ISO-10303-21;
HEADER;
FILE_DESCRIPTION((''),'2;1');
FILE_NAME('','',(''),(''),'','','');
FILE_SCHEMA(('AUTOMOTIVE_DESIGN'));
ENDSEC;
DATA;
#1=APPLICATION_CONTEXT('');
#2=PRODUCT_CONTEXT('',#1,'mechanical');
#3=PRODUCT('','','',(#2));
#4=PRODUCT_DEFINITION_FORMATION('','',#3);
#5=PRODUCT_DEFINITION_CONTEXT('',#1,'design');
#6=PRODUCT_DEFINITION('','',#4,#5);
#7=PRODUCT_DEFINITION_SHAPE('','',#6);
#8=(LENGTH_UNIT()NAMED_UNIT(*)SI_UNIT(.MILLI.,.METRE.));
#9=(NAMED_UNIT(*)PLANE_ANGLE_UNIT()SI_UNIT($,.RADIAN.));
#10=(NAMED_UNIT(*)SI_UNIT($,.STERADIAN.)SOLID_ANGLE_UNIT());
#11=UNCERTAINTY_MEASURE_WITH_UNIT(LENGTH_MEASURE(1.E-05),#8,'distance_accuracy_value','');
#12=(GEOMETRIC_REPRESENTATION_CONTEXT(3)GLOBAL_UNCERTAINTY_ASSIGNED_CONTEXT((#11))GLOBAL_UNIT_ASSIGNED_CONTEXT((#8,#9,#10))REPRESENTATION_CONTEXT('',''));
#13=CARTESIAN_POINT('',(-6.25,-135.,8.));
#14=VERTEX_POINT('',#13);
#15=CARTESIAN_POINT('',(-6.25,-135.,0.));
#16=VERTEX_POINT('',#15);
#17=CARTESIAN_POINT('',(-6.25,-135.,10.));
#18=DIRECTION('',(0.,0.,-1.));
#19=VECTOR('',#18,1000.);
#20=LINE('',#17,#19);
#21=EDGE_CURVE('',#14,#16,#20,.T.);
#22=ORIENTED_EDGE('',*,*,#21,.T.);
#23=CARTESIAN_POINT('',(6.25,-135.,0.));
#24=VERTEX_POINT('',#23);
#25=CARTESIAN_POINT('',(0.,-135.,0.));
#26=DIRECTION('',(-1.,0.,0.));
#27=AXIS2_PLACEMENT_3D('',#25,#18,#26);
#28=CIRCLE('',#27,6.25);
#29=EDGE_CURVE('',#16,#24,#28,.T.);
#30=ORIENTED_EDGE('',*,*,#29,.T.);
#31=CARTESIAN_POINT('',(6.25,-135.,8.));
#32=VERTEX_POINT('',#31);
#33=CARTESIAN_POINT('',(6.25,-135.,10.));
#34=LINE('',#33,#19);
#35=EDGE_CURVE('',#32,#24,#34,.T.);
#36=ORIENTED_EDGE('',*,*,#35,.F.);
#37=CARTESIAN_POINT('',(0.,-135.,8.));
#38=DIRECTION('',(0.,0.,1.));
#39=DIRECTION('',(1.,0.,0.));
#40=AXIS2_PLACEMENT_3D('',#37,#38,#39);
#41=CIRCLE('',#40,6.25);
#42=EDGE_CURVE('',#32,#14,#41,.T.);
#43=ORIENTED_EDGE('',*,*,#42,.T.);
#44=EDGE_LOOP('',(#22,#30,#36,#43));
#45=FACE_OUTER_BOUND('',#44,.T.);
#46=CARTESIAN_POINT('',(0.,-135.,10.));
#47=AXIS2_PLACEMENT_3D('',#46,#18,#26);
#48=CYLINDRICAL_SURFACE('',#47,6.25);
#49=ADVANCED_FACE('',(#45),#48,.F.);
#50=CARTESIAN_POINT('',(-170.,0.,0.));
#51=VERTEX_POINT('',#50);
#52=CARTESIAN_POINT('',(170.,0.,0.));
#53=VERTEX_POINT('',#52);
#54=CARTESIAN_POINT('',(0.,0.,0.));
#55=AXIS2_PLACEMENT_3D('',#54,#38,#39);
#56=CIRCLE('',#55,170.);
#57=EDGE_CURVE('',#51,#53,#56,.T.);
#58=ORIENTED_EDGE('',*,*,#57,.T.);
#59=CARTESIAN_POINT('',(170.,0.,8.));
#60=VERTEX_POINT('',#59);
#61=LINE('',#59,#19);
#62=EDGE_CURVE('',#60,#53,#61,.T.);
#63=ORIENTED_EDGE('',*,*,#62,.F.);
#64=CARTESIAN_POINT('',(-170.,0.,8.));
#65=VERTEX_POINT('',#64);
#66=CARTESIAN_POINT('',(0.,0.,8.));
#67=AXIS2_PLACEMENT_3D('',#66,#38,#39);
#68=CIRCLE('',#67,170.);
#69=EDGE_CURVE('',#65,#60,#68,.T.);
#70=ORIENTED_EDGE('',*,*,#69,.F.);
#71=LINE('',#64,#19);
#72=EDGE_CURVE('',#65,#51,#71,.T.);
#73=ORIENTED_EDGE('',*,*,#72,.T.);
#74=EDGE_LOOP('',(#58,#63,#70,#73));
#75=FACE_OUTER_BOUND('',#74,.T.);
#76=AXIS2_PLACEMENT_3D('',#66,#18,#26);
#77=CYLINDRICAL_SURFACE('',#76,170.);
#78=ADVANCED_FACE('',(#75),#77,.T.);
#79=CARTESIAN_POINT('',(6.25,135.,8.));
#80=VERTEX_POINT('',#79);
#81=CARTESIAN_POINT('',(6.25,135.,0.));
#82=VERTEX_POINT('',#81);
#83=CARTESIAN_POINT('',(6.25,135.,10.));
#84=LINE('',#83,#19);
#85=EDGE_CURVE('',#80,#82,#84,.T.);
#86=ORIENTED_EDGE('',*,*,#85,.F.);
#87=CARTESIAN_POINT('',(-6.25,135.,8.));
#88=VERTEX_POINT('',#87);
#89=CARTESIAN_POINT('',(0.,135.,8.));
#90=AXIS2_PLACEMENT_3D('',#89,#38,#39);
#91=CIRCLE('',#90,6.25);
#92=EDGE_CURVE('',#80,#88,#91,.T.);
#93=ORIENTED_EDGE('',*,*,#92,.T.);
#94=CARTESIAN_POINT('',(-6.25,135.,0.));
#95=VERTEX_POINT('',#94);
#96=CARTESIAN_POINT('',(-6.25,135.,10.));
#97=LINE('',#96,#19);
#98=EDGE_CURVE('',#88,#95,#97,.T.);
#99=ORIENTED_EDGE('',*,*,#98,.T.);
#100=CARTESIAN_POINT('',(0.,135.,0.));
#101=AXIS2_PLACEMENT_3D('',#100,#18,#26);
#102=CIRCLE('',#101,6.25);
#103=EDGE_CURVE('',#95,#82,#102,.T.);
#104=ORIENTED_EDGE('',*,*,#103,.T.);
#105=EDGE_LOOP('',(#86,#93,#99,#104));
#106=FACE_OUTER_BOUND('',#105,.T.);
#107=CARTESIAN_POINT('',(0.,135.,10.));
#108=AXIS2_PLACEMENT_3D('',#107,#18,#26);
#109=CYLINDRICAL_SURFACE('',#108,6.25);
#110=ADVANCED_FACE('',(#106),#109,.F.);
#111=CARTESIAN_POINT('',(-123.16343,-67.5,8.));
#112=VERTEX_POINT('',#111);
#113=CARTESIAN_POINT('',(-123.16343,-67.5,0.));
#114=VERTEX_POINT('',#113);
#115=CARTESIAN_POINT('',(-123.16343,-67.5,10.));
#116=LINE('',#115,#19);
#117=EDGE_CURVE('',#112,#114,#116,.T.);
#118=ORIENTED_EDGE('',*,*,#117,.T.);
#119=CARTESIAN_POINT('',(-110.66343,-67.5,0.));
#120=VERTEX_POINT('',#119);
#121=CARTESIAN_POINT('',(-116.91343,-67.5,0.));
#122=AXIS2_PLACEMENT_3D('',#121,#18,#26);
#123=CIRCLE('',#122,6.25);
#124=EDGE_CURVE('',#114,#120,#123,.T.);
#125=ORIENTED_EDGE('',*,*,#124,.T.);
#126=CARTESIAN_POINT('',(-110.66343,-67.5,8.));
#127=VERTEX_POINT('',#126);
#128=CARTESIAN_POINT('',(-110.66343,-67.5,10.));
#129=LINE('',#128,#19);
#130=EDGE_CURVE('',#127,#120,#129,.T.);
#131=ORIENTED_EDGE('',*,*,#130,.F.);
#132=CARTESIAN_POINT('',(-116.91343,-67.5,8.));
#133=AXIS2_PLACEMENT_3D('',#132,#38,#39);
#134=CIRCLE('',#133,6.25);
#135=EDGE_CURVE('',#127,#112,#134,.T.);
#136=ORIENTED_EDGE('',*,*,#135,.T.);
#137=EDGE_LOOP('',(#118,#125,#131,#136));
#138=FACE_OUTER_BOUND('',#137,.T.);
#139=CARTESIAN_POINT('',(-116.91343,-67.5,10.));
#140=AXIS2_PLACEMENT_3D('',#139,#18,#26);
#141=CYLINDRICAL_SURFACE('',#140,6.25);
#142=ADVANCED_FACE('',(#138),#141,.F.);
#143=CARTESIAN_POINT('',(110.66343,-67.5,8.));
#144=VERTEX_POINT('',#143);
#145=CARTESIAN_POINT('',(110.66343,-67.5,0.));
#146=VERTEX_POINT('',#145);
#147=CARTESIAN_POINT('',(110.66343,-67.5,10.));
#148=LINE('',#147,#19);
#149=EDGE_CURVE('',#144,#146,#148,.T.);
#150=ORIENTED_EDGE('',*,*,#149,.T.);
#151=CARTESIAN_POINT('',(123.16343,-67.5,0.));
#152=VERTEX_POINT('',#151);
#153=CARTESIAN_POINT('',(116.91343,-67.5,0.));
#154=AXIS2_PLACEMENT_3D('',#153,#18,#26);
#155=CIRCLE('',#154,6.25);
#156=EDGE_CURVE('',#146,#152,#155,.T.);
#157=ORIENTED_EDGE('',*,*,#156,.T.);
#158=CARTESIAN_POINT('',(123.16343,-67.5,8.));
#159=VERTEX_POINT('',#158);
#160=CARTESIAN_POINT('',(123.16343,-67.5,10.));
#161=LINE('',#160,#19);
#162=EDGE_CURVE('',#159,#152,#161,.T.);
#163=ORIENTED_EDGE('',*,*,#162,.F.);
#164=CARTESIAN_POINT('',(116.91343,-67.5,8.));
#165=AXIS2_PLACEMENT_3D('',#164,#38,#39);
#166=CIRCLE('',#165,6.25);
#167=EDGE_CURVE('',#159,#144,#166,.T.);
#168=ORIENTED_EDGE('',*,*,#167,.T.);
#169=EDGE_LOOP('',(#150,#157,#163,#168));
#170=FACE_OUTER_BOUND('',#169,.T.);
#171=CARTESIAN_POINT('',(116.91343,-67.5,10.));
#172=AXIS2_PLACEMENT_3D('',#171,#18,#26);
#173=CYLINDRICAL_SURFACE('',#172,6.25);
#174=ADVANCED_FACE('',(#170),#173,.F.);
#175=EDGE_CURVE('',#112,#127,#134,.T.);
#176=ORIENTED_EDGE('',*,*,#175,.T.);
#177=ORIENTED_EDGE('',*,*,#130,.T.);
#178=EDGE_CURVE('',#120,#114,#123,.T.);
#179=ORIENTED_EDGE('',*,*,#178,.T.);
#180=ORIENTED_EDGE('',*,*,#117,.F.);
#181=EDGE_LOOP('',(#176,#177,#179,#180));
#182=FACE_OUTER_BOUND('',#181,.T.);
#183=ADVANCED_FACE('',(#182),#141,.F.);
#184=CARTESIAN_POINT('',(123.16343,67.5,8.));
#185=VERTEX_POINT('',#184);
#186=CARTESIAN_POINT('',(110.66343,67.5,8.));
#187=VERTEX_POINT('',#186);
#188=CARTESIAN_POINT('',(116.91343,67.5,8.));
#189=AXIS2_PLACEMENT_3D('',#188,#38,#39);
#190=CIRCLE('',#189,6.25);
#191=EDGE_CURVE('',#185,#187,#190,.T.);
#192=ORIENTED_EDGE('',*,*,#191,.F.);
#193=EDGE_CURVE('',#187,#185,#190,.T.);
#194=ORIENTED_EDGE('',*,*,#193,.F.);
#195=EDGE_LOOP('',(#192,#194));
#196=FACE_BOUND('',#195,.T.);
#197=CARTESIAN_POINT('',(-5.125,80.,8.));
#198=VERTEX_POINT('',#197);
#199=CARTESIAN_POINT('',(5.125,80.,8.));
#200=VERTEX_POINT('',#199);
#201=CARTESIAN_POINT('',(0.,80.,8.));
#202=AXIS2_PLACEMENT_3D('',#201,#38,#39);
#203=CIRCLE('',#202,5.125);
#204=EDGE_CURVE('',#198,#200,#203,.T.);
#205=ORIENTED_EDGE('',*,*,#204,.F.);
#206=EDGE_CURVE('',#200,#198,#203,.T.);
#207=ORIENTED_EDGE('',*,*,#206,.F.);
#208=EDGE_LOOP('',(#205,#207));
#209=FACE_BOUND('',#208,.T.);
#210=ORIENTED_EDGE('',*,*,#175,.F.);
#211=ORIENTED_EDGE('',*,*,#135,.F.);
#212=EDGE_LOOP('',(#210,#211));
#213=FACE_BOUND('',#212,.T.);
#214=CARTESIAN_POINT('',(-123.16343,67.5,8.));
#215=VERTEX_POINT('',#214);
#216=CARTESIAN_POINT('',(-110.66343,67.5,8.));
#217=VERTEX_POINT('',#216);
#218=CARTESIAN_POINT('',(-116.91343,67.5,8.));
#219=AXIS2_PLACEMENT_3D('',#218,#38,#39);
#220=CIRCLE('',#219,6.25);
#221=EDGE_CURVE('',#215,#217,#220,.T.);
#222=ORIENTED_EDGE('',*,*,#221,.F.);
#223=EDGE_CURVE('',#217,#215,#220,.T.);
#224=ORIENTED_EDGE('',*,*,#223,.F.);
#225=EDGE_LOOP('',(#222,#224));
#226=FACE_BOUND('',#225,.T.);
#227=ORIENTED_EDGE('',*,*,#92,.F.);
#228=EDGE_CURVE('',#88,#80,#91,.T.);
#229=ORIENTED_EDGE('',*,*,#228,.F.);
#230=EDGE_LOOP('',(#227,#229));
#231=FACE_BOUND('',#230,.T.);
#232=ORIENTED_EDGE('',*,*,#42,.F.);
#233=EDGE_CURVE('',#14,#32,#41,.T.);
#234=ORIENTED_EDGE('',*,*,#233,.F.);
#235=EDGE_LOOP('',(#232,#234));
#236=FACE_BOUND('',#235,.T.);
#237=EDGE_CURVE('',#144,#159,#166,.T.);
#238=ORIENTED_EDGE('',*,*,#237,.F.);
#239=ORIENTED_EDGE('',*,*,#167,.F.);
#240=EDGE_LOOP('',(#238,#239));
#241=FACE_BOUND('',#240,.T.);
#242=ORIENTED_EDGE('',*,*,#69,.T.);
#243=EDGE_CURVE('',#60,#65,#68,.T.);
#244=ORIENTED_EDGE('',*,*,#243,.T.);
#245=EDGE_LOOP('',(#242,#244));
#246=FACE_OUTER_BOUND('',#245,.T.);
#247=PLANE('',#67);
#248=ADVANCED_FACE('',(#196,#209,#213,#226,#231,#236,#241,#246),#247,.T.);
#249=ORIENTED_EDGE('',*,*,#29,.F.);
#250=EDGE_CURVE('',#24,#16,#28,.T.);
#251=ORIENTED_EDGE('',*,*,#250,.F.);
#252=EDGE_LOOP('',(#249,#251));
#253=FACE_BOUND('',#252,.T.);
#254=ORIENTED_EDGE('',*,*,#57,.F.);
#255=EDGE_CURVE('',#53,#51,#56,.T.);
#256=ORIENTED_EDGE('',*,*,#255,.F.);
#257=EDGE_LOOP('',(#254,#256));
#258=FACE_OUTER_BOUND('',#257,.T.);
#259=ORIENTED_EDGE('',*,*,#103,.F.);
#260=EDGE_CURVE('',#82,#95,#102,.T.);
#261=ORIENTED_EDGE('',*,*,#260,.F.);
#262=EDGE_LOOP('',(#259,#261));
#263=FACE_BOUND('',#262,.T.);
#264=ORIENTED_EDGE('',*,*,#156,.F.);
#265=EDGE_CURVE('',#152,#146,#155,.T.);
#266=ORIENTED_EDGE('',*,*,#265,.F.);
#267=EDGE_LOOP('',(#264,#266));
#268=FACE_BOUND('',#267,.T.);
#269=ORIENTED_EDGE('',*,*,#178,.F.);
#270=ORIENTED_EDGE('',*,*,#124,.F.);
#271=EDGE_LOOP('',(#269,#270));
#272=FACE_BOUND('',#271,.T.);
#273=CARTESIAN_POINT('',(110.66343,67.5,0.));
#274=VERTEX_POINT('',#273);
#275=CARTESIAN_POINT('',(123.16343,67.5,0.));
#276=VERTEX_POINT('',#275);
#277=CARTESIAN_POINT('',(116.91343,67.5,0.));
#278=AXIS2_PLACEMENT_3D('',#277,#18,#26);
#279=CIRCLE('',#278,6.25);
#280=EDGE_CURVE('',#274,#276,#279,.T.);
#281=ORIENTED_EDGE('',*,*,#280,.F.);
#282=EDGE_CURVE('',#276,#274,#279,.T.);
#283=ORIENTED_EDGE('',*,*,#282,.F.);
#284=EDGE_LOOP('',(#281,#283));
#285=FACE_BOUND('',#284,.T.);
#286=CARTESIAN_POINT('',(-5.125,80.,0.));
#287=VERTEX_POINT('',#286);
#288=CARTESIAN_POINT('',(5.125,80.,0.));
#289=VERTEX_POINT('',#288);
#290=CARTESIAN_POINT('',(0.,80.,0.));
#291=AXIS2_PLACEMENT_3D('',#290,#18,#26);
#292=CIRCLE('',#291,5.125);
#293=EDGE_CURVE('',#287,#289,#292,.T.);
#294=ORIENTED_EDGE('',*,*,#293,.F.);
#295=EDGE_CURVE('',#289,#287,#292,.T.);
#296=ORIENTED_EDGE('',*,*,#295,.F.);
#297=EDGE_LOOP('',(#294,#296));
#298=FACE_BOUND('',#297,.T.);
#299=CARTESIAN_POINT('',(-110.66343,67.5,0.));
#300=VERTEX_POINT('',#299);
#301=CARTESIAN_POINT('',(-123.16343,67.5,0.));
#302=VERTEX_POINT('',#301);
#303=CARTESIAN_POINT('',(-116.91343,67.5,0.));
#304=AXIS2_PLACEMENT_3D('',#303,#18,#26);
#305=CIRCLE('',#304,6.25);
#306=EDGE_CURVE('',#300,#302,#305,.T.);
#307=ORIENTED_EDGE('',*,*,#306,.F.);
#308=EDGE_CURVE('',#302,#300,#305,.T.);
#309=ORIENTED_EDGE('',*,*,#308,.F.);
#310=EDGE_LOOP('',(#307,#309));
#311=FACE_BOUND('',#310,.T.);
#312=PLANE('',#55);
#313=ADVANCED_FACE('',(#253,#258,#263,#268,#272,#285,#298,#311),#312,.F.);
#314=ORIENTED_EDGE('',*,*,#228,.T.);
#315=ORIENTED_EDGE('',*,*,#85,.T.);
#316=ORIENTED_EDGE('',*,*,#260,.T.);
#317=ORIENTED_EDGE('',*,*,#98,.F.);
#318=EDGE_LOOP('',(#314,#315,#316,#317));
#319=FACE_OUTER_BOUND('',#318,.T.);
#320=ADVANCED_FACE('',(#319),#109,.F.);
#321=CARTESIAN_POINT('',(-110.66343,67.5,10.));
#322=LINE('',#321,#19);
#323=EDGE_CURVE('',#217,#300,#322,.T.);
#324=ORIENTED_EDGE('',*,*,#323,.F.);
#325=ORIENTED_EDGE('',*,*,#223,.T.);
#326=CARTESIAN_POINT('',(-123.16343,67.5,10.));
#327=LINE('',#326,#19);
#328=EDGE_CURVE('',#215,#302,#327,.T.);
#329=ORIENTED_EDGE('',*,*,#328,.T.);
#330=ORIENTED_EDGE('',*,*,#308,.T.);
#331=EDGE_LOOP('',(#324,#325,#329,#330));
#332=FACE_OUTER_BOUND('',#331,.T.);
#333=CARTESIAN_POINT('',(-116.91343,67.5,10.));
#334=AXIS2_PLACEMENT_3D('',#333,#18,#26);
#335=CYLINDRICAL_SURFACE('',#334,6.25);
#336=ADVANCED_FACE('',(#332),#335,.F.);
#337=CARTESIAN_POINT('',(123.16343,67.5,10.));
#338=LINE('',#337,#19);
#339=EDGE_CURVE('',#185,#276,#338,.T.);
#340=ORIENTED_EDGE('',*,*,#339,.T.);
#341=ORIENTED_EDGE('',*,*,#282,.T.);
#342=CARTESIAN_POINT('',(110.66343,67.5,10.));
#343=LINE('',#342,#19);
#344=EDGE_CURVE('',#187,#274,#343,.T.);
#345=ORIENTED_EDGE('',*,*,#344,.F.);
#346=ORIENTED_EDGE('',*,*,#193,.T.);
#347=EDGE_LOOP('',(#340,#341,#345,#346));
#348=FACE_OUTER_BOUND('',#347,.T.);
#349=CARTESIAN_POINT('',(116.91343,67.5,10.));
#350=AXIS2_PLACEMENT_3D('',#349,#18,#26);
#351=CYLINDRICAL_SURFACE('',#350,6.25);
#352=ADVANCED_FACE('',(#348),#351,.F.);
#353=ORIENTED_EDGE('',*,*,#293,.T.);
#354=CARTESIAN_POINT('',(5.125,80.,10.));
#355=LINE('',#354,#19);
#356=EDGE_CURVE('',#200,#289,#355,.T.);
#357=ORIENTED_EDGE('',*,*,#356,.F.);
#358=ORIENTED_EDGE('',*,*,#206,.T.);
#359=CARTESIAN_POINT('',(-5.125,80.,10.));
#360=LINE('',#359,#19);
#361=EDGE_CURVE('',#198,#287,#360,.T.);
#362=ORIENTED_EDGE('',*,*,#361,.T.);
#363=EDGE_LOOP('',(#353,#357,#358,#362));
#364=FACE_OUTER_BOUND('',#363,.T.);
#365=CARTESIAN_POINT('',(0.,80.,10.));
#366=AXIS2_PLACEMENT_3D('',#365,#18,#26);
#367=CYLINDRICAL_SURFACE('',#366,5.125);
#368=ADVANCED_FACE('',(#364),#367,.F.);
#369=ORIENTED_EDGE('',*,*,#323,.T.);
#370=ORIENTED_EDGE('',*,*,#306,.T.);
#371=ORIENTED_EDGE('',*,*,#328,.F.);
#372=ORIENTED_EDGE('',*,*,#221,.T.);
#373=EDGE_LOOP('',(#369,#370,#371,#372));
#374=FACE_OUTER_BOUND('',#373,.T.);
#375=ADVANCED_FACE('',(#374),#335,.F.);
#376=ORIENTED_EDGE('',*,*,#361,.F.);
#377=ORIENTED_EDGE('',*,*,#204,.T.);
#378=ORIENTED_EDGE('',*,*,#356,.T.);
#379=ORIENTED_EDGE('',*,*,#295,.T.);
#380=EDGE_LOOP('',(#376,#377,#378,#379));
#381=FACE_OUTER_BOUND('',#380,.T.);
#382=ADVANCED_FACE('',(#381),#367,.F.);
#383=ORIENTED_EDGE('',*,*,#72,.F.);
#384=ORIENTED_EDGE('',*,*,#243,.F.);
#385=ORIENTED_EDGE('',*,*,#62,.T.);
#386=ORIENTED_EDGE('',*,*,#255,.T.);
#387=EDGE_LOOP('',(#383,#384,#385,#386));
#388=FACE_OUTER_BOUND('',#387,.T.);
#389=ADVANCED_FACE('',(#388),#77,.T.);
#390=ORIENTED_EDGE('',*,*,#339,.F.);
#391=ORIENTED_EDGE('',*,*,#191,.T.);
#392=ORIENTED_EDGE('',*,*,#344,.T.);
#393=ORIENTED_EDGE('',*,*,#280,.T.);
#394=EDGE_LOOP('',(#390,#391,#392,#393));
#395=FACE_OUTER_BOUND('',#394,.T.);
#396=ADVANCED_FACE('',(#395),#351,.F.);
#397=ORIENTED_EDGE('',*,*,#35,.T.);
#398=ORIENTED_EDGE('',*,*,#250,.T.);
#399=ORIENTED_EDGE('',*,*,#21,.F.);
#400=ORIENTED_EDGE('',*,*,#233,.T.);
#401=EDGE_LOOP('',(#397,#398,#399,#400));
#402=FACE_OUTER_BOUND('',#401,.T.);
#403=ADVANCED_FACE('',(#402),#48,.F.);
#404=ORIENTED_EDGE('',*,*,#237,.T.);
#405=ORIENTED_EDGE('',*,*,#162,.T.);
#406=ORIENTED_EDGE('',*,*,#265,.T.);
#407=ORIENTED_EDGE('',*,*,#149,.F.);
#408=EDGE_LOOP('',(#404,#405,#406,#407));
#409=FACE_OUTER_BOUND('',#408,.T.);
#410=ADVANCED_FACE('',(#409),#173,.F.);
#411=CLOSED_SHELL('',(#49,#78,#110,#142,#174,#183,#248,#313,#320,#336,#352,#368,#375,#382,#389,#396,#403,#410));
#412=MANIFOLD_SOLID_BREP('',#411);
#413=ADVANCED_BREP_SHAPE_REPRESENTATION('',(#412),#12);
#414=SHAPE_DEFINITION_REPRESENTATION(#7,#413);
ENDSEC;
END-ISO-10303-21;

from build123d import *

# Parameters (mm, degrees)
SKETCH1_R           = 170
BOSS_EXTRUDE1_DEPTH = 8
SKETCH3_R           = 6.25
CUT_EXTRUDE1_DEPTH  = 10
SKETCH4_R           = 5.125
CUT_EXTRUDE2_DEPTH  = 10


with BuildPart() as part:
    # Sketch1 → Boss-Extrude1 (new body)
    with BuildSketch(Plane.XY):
        Circle(SKETCH1_R)
    extrude(amount=BOSS_EXTRUDE1_DEPTH)

    # Sketch3 → Cut-Extrude1 (cut)
    with BuildSketch(Plane(origin=(0, 0, 0), x_dir=(-1, 0, 0), z_dir=(0, 0, -1))):
        with Locations((116.913429511, 67.5)):
            Circle(SKETCH3_R)
        with Locations((0, 135)):
            Circle(SKETCH3_R)
        with Locations((116.913429511, -67.5)):
            Circle(SKETCH3_R)
        with Locations((0, -135)):
            Circle(SKETCH3_R)
        with Locations((-116.913429511, -67.5)):
            Circle(SKETCH3_R)
        with Locations((-116.913429511, 67.5)):
            Circle(SKETCH3_R)
    extrude(amount=-CUT_EXTRUDE1_DEPTH, mode=Mode.SUBTRACT)

    # Sketch4 → Cut-Extrude2 (cut)
    with BuildSketch(Plane(origin=(0, 0, 0), x_dir=(-1, 0, 0), z_dir=(0, 0, -1))):
        with Locations((0, 80)):
            Circle(SKETCH4_R)
    extrude(amount=-CUT_EXTRUDE2_DEPTH, mode=Mode.SUBTRACT)


solid = part.part
